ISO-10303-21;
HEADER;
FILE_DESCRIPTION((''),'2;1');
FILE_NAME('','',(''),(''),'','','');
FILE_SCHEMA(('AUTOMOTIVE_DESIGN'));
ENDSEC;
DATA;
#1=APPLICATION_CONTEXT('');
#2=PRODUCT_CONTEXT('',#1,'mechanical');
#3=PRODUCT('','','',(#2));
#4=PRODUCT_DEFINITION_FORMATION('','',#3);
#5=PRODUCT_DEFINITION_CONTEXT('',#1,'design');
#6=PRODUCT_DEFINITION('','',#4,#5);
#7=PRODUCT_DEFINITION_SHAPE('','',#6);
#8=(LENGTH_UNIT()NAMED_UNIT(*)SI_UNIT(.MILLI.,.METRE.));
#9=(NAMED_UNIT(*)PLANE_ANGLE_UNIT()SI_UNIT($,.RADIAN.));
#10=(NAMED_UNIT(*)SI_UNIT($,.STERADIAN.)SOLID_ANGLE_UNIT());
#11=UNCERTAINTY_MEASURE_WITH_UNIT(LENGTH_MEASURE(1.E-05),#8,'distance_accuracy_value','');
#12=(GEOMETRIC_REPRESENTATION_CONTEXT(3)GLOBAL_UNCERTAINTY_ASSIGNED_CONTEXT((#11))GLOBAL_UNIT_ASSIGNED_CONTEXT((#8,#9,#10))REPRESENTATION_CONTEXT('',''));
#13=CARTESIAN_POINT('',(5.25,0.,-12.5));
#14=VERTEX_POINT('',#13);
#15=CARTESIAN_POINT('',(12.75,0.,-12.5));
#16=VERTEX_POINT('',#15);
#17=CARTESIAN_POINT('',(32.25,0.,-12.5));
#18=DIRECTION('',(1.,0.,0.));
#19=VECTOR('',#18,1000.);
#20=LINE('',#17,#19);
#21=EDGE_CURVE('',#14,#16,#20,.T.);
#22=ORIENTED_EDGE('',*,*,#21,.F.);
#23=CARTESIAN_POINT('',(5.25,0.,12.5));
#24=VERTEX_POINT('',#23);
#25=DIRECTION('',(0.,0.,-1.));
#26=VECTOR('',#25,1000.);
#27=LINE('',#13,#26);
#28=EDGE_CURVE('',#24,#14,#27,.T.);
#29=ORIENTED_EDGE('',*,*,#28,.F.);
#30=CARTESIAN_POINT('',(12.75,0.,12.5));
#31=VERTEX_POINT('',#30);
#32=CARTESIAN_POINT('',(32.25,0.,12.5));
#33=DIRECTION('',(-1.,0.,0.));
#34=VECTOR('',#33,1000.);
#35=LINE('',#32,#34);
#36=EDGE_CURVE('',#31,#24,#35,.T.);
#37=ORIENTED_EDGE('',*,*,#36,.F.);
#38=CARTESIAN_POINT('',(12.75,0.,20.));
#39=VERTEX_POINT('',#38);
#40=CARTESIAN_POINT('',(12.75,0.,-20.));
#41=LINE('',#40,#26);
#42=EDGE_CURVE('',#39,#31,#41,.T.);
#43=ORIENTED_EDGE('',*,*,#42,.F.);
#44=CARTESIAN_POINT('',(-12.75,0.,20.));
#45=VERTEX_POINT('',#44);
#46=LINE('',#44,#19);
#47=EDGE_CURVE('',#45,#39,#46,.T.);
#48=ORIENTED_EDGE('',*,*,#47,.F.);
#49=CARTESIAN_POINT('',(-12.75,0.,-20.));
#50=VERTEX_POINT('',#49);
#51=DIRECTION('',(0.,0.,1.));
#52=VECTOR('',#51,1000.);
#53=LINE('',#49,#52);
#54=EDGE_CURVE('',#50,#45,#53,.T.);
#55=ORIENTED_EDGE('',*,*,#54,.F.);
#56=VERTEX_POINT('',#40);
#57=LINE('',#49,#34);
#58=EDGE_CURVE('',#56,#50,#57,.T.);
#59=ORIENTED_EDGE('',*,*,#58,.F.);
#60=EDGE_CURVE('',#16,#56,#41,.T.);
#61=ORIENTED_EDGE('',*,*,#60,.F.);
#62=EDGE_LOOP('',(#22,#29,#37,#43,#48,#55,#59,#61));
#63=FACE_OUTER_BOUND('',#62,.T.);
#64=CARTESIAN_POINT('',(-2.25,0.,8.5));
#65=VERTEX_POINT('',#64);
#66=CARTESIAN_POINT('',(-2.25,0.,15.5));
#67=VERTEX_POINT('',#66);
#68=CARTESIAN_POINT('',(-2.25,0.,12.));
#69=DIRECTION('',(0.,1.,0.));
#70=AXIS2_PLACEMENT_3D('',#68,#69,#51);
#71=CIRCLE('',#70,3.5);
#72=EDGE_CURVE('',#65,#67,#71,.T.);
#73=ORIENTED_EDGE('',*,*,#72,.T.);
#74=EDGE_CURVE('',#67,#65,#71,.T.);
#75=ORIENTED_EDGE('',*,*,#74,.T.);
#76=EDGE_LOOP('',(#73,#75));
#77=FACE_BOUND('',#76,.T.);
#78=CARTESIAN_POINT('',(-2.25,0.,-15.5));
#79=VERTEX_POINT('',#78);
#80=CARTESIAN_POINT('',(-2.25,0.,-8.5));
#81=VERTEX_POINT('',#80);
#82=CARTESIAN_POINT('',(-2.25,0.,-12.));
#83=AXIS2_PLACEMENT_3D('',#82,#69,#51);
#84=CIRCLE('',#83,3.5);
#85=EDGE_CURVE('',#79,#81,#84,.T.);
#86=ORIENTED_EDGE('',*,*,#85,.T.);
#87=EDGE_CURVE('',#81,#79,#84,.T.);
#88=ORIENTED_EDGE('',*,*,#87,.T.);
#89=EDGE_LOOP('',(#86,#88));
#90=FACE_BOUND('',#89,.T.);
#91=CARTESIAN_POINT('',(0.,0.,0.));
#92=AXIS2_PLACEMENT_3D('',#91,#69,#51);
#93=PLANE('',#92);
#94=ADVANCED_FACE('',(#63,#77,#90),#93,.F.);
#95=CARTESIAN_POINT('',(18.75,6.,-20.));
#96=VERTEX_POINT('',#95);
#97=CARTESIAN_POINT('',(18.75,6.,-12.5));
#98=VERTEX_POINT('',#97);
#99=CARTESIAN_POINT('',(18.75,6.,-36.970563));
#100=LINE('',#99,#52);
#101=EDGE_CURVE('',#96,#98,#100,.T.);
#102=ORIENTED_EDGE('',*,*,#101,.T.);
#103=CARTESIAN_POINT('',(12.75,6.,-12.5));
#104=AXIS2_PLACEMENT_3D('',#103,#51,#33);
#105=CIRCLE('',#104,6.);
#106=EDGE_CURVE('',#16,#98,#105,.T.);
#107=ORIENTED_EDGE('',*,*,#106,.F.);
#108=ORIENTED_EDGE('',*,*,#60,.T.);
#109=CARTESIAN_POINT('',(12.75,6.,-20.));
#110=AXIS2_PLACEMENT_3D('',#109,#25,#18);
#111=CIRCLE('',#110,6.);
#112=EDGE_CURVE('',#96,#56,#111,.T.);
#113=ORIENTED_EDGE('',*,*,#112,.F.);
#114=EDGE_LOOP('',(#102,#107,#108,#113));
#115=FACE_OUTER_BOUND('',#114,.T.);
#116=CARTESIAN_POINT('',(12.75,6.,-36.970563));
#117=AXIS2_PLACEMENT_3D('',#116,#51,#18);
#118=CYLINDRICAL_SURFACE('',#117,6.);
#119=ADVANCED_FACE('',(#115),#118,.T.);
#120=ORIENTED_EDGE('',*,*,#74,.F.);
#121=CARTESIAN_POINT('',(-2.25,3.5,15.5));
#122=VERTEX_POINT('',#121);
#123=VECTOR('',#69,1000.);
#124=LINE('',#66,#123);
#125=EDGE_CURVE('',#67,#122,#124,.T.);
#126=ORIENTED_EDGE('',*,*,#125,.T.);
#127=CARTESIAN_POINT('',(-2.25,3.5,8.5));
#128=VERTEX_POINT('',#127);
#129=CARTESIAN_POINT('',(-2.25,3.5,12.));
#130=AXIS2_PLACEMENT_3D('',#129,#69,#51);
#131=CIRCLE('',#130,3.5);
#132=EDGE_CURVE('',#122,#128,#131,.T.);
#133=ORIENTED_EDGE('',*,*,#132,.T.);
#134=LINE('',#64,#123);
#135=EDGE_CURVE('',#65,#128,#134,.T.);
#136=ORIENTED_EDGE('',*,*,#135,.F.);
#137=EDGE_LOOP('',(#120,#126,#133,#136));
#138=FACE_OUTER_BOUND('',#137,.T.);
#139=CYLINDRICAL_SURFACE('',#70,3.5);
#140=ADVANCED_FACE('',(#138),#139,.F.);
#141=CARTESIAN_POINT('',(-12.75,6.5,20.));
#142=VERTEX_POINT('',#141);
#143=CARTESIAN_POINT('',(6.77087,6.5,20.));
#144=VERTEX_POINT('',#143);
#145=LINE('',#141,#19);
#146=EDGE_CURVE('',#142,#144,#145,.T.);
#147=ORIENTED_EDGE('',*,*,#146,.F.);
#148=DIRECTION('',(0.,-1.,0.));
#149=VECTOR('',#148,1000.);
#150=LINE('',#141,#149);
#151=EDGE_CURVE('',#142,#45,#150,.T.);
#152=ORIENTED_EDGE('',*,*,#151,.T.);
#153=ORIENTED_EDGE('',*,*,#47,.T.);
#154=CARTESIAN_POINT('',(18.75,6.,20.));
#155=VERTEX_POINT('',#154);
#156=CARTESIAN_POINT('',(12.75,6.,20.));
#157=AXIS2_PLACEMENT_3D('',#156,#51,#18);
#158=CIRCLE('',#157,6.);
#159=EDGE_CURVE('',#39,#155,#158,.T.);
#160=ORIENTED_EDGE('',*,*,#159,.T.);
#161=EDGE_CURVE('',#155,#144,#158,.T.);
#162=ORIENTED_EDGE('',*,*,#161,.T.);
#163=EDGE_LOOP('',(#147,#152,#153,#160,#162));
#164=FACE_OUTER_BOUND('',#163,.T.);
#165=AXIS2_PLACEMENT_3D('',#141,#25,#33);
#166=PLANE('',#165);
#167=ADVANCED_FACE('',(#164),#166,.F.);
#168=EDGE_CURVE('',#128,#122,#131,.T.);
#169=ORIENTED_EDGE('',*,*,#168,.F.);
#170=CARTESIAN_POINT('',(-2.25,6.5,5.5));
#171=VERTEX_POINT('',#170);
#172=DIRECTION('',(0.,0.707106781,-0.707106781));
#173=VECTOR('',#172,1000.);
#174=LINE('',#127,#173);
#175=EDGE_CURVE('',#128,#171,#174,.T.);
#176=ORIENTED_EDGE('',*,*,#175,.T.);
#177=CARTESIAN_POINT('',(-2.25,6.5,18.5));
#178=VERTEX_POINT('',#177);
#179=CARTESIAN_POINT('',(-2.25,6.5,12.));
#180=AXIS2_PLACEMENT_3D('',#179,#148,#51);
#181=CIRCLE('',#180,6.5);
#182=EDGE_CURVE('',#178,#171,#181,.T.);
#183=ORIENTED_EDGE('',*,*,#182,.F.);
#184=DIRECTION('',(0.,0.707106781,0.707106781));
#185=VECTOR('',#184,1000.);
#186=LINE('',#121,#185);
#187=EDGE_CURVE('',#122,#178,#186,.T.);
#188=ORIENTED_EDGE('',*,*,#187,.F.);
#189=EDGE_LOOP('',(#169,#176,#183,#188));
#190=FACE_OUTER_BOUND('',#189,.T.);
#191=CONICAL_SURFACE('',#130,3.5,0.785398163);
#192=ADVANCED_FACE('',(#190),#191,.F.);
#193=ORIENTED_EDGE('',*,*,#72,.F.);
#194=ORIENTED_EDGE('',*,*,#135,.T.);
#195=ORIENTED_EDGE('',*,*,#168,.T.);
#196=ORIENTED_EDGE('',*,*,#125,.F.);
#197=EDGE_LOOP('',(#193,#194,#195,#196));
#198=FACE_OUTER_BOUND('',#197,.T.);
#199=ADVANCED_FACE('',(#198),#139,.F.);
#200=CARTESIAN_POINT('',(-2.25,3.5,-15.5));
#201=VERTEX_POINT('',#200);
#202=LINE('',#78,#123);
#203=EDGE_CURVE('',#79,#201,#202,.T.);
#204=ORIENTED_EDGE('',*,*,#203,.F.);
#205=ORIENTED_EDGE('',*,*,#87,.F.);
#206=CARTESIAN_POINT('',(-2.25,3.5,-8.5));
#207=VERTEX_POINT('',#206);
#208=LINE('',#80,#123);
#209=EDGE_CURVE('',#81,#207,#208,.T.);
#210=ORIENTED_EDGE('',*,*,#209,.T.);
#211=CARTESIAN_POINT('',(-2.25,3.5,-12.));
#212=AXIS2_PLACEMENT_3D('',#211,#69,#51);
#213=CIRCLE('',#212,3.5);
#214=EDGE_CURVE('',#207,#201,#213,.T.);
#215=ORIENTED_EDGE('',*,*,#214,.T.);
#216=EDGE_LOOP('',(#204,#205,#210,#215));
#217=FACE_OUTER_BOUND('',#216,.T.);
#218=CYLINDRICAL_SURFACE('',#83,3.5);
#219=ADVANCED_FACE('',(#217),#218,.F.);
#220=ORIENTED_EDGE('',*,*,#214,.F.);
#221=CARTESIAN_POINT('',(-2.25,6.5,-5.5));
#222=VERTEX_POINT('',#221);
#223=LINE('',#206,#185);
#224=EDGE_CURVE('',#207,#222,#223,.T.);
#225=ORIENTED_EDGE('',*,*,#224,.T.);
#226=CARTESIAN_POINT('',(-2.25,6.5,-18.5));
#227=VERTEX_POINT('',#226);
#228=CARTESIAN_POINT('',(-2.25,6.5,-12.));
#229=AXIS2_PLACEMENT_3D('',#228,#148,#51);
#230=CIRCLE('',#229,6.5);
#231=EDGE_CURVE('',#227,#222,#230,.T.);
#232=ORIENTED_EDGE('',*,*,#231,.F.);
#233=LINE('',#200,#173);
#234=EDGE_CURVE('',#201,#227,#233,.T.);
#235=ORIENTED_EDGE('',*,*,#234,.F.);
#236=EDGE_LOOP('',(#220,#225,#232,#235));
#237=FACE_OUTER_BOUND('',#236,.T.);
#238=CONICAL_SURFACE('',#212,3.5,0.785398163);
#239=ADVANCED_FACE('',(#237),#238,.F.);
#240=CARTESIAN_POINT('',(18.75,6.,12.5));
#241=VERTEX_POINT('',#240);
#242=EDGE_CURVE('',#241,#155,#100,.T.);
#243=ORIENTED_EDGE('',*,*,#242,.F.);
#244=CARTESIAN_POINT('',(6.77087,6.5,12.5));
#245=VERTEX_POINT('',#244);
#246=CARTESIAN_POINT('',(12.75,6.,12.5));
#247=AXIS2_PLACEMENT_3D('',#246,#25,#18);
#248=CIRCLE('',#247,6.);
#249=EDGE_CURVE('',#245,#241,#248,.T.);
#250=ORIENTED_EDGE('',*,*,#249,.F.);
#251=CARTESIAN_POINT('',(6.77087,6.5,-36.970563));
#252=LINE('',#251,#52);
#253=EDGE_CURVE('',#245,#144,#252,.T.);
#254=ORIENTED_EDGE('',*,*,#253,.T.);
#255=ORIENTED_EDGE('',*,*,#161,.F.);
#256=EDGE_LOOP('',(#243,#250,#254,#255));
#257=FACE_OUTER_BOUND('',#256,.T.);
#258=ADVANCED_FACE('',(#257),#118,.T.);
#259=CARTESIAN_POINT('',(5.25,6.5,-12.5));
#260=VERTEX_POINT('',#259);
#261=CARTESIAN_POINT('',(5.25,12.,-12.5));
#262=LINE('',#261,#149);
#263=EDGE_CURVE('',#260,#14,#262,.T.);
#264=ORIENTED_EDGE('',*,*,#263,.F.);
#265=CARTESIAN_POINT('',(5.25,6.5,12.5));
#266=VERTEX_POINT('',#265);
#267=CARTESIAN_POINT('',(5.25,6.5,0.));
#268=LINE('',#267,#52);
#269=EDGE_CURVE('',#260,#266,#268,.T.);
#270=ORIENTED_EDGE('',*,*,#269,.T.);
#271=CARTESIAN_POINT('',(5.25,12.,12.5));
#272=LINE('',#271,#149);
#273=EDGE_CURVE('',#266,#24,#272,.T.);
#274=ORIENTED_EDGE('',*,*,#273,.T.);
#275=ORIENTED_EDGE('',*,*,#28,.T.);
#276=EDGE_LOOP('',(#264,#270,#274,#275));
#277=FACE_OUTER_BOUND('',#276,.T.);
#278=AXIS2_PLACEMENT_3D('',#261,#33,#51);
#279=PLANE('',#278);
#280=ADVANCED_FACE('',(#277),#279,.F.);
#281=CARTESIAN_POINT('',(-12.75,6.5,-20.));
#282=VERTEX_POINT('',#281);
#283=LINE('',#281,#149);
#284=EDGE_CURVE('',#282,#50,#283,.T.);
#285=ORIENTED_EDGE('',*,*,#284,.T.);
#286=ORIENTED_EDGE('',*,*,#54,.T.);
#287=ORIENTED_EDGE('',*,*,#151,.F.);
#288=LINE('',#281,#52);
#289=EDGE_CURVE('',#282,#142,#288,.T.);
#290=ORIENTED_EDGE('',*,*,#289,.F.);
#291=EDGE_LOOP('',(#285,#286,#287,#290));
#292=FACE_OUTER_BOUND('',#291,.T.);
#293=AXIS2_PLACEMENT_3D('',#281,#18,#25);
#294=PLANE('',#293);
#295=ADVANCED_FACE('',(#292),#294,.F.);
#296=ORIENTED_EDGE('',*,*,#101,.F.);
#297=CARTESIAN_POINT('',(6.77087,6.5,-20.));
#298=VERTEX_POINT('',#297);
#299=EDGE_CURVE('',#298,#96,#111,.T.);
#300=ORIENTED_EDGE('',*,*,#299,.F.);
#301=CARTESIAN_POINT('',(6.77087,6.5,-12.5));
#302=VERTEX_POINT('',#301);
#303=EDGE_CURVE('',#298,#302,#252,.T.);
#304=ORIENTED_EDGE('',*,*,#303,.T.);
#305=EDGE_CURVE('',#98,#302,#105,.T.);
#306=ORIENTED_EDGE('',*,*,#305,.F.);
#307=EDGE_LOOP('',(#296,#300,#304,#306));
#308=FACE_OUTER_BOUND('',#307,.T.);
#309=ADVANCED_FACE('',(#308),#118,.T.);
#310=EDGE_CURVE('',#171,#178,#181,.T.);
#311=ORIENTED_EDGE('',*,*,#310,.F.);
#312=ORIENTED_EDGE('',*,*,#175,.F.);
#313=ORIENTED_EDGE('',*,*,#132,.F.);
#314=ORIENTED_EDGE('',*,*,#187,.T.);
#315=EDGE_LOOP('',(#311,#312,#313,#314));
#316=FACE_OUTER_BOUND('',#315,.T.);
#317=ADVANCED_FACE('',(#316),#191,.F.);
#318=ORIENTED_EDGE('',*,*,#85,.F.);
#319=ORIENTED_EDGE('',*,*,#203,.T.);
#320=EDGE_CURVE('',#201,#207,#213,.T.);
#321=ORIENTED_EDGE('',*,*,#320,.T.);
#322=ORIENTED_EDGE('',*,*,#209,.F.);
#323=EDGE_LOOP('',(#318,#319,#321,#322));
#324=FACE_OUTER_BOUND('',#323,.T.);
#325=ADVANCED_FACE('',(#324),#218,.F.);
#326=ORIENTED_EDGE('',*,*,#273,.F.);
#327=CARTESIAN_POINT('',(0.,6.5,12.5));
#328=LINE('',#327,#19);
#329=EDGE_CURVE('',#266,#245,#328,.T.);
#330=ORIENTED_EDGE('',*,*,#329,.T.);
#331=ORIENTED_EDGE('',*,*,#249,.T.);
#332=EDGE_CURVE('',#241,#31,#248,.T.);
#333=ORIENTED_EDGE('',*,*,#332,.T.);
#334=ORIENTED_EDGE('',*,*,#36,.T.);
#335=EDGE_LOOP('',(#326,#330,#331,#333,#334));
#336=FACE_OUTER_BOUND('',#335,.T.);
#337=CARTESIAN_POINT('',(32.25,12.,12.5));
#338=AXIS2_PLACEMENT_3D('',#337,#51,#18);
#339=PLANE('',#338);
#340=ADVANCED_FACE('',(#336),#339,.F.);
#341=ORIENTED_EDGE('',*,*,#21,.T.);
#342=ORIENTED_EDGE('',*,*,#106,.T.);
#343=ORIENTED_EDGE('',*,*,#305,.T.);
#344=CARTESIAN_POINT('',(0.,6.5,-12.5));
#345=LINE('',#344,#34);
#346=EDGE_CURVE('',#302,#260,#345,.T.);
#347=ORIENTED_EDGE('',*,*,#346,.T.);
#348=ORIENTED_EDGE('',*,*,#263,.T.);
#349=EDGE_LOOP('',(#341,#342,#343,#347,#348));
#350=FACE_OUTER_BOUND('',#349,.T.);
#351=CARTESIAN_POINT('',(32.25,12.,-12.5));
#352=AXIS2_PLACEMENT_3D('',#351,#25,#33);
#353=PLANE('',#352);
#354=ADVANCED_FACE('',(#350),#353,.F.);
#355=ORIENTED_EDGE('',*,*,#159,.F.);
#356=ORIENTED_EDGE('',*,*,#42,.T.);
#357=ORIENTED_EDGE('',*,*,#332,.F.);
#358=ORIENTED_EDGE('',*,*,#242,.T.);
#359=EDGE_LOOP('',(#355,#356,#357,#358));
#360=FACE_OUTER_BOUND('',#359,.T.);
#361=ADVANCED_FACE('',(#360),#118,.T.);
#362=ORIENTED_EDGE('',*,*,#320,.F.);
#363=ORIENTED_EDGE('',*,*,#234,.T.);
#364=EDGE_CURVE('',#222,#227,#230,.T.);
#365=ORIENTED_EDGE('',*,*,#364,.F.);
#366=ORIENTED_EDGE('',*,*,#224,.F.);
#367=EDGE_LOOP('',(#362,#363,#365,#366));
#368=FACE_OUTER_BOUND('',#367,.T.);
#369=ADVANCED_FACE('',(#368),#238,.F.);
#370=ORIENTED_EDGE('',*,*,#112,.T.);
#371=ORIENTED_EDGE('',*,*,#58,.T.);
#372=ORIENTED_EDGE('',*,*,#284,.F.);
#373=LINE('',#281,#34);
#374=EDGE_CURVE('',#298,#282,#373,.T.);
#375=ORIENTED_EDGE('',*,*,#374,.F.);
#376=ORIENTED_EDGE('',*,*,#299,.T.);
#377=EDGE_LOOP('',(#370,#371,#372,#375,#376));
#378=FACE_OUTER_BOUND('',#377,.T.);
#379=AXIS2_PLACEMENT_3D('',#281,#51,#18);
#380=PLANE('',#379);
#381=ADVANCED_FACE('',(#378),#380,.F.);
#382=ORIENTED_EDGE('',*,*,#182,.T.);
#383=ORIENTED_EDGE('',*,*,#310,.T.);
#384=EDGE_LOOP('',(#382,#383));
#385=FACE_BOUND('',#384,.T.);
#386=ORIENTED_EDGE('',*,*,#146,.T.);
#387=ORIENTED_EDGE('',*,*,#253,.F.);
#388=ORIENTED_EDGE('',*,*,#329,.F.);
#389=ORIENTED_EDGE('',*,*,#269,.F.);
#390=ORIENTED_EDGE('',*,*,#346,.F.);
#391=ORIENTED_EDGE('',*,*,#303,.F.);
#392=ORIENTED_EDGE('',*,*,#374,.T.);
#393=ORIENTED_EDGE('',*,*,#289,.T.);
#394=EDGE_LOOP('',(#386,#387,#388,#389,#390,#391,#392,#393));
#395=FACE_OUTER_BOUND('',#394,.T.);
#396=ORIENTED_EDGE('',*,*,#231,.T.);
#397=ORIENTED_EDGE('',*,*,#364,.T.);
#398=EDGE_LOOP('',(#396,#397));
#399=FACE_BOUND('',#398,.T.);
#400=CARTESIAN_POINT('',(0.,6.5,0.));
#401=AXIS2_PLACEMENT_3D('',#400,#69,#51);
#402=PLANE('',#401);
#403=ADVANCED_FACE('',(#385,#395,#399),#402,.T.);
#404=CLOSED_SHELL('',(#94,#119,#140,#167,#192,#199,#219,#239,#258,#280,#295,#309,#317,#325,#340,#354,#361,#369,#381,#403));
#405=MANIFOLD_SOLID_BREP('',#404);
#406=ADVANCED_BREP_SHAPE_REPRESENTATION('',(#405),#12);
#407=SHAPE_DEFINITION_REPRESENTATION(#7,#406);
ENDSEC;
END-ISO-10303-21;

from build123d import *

# Parameters (mm, degrees)
SKETCH_1_W          = 25.5
SKETCH_1_H          = 40
EXTRUDE_1_DEPTH     = 6.5
SKETCH_2_R          = 6
EXTRUDE_2_DEPTH     = 40
SKETCH_3_W          = 27
SKETCH_3_H          = 25
CUT_EXTRUDE_1_DEPTH = 30.925950277
SKETCH_5_R          = 3.5
CUT_EXTRUDE_2_DEPTH = 29.174678348
CHAMFER_1_SIZE      = 3


with BuildPart() as part:
    # 草图1 → 凸台-拉伸1 (new body)
    with BuildSketch(Plane(origin=(0, 0, 0), x_dir=(1, 0, 0), z_dir=(0, 1, 0))):
        Rectangle(SKETCH_1_W, SKETCH_1_H)
    extrude(amount=EXTRUDE_1_DEPTH)

    # 草图2 → 凸台-拉伸2 (add)
    with BuildSketch(Plane.XY.offset(20)):
        with Locations((12.75, 6)):
            Circle(SKETCH_2_R)
    extrude(amount=-EXTRUDE_2_DEPTH)

    # 草图3 → 切除-拉伸1 (cut, through all)
    with BuildSketch(Plane.XZ):
        with Locations((18.75, 0)):
            Rectangle(SKETCH_3_W, SKETCH_3_H)
    extrude(amount=-CUT_EXTRUDE_1_DEPTH, mode=Mode.SUBTRACT)

    # 草图5 → 切除-拉伸2 (cut, through all)
    with BuildSketch(Plane(origin=(0, 6.5, 0), x_dir=(1, 0, 0), z_dir=(0, 1, 0))):
        with Locations(Location((-2.25, 12, 0), (0, 0, 270))):
            Circle(SKETCH_5_R)
        with Locations(Location((-2.25, -12, 0), (0, 0, 270))):
            Circle(SKETCH_5_R)
    extrude(amount=-CUT_EXTRUDE_2_DEPTH, mode=Mode.SUBTRACT)

    # 倒角1
    chamfer_1_edges = [part.edges().sort_by_distance(p)[0] for p in [
        (-2.25, 6.5, -15.5),
        (-2.25, 6.5, 8.5),
    ]]
    chamfer(chamfer_1_edges, length=CHAMFER_1_SIZE)


solid = part.part
